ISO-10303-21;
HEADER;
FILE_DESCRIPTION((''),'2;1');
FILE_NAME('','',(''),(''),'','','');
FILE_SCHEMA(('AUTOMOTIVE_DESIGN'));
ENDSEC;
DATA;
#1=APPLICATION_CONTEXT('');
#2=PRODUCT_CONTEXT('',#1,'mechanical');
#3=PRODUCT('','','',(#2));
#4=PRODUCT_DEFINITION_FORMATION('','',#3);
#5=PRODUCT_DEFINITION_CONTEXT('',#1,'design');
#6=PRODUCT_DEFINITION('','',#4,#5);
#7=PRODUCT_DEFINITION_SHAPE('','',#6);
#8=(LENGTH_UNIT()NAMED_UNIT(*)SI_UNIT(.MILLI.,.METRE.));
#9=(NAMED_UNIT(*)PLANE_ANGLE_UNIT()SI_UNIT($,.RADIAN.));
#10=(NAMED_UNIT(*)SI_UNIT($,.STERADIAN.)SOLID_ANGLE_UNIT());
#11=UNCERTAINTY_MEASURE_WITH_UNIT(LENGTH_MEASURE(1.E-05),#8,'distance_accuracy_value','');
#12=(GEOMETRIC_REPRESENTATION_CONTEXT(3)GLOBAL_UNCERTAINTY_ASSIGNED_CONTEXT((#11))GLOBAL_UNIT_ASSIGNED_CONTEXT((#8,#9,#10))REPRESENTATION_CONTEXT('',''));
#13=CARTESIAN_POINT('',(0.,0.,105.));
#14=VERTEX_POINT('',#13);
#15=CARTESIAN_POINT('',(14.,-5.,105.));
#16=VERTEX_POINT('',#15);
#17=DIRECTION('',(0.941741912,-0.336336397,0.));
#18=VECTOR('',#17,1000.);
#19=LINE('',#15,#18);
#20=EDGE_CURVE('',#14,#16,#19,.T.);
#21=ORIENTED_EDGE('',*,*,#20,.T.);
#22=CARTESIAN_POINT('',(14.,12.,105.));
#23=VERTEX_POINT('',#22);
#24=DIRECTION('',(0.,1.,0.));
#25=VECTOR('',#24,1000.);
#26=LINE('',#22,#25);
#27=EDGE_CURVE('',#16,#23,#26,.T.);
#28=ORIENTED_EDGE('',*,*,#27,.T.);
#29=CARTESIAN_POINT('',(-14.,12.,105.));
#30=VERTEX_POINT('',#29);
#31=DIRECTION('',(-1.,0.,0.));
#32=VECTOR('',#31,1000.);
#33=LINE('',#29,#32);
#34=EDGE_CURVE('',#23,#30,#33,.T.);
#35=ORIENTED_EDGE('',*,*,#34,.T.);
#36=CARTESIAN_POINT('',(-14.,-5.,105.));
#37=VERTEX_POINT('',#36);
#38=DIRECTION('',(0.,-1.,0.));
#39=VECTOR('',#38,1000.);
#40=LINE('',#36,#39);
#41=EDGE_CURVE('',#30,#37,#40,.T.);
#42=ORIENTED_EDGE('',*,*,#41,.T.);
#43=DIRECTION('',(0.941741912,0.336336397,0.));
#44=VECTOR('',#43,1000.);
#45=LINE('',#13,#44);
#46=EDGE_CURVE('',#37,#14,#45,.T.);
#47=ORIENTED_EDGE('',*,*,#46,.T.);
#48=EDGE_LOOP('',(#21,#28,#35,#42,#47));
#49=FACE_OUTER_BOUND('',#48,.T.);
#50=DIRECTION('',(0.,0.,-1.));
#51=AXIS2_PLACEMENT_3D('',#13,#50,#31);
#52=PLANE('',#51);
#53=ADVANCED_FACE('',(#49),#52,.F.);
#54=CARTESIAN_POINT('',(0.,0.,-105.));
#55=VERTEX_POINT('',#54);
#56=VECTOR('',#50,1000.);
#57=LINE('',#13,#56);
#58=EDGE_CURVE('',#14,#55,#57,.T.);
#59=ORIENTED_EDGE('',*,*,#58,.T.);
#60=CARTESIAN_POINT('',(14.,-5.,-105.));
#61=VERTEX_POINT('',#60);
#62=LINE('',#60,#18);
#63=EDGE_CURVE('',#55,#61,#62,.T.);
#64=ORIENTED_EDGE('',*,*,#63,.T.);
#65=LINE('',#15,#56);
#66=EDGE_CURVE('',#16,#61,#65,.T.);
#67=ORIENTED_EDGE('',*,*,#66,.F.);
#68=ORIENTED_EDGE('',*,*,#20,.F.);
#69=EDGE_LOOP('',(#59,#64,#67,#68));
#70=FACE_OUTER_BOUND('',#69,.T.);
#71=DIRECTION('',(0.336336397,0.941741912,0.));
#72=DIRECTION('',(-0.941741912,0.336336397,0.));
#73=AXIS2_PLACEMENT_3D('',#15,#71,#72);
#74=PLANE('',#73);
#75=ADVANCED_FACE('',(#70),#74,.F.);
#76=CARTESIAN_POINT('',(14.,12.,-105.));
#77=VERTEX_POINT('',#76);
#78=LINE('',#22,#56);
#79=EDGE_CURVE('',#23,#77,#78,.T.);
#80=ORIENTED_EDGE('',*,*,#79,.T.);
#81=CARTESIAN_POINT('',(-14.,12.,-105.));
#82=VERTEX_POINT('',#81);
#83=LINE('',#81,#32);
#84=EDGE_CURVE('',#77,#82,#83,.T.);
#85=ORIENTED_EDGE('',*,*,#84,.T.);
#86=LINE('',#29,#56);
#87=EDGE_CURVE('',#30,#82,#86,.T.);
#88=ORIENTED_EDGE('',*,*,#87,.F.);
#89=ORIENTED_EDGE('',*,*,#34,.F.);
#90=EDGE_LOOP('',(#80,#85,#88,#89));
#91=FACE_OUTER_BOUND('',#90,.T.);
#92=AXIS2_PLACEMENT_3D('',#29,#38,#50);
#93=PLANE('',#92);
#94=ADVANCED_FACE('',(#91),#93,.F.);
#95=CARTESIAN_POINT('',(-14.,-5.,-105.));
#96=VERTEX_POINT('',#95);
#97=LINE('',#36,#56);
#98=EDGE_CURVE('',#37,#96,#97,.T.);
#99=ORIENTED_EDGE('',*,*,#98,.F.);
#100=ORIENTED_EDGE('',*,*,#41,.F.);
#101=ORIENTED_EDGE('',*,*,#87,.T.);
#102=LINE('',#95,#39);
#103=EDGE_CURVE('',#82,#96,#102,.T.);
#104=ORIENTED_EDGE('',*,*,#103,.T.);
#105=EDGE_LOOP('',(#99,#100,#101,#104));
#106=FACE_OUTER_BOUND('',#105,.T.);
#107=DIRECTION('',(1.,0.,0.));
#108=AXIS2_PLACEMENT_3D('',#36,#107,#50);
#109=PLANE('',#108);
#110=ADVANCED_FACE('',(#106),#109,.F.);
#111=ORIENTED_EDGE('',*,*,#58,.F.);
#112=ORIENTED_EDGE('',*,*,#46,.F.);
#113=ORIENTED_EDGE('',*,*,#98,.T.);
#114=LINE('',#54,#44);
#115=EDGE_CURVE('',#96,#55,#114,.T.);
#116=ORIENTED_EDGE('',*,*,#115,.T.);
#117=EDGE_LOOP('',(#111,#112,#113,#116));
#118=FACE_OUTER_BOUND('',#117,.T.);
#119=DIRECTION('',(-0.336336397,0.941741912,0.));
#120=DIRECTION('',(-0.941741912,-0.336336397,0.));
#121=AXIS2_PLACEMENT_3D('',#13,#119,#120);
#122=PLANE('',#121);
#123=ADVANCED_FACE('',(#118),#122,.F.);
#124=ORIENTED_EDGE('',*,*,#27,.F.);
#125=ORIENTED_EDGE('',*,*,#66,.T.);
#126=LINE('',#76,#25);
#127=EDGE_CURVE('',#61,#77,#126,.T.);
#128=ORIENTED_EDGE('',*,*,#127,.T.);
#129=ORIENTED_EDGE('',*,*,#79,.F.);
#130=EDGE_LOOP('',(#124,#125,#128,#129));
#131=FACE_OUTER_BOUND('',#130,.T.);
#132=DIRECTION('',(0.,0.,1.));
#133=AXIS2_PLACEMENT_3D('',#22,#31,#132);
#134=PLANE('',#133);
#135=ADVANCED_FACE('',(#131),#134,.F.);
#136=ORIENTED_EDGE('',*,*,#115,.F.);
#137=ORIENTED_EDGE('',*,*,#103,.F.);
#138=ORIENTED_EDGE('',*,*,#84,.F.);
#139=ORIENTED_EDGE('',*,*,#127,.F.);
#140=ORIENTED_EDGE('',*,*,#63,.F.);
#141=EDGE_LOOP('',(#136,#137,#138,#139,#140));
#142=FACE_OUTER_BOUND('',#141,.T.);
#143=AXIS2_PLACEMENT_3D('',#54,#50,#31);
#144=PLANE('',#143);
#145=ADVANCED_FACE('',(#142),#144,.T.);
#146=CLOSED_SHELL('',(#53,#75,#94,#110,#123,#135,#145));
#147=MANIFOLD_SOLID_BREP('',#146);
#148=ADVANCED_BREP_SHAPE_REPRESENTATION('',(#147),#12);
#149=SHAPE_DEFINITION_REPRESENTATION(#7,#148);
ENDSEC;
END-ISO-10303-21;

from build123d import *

# Parameters (mm, degrees)
EXTRUDE_1_DEPTH = 105


with BuildPart() as part:
    # 草图1 → 凸台-拉伸1 (new, symmetric)
    with BuildSketch(Plane.XY):
        Polygon((0, 0), (-14, -5), (-14, 12), (14, 12), (14, -5), align=None)
    extrude(amount=EXTRUDE_1_DEPTH, both=True)


solid = part.part
